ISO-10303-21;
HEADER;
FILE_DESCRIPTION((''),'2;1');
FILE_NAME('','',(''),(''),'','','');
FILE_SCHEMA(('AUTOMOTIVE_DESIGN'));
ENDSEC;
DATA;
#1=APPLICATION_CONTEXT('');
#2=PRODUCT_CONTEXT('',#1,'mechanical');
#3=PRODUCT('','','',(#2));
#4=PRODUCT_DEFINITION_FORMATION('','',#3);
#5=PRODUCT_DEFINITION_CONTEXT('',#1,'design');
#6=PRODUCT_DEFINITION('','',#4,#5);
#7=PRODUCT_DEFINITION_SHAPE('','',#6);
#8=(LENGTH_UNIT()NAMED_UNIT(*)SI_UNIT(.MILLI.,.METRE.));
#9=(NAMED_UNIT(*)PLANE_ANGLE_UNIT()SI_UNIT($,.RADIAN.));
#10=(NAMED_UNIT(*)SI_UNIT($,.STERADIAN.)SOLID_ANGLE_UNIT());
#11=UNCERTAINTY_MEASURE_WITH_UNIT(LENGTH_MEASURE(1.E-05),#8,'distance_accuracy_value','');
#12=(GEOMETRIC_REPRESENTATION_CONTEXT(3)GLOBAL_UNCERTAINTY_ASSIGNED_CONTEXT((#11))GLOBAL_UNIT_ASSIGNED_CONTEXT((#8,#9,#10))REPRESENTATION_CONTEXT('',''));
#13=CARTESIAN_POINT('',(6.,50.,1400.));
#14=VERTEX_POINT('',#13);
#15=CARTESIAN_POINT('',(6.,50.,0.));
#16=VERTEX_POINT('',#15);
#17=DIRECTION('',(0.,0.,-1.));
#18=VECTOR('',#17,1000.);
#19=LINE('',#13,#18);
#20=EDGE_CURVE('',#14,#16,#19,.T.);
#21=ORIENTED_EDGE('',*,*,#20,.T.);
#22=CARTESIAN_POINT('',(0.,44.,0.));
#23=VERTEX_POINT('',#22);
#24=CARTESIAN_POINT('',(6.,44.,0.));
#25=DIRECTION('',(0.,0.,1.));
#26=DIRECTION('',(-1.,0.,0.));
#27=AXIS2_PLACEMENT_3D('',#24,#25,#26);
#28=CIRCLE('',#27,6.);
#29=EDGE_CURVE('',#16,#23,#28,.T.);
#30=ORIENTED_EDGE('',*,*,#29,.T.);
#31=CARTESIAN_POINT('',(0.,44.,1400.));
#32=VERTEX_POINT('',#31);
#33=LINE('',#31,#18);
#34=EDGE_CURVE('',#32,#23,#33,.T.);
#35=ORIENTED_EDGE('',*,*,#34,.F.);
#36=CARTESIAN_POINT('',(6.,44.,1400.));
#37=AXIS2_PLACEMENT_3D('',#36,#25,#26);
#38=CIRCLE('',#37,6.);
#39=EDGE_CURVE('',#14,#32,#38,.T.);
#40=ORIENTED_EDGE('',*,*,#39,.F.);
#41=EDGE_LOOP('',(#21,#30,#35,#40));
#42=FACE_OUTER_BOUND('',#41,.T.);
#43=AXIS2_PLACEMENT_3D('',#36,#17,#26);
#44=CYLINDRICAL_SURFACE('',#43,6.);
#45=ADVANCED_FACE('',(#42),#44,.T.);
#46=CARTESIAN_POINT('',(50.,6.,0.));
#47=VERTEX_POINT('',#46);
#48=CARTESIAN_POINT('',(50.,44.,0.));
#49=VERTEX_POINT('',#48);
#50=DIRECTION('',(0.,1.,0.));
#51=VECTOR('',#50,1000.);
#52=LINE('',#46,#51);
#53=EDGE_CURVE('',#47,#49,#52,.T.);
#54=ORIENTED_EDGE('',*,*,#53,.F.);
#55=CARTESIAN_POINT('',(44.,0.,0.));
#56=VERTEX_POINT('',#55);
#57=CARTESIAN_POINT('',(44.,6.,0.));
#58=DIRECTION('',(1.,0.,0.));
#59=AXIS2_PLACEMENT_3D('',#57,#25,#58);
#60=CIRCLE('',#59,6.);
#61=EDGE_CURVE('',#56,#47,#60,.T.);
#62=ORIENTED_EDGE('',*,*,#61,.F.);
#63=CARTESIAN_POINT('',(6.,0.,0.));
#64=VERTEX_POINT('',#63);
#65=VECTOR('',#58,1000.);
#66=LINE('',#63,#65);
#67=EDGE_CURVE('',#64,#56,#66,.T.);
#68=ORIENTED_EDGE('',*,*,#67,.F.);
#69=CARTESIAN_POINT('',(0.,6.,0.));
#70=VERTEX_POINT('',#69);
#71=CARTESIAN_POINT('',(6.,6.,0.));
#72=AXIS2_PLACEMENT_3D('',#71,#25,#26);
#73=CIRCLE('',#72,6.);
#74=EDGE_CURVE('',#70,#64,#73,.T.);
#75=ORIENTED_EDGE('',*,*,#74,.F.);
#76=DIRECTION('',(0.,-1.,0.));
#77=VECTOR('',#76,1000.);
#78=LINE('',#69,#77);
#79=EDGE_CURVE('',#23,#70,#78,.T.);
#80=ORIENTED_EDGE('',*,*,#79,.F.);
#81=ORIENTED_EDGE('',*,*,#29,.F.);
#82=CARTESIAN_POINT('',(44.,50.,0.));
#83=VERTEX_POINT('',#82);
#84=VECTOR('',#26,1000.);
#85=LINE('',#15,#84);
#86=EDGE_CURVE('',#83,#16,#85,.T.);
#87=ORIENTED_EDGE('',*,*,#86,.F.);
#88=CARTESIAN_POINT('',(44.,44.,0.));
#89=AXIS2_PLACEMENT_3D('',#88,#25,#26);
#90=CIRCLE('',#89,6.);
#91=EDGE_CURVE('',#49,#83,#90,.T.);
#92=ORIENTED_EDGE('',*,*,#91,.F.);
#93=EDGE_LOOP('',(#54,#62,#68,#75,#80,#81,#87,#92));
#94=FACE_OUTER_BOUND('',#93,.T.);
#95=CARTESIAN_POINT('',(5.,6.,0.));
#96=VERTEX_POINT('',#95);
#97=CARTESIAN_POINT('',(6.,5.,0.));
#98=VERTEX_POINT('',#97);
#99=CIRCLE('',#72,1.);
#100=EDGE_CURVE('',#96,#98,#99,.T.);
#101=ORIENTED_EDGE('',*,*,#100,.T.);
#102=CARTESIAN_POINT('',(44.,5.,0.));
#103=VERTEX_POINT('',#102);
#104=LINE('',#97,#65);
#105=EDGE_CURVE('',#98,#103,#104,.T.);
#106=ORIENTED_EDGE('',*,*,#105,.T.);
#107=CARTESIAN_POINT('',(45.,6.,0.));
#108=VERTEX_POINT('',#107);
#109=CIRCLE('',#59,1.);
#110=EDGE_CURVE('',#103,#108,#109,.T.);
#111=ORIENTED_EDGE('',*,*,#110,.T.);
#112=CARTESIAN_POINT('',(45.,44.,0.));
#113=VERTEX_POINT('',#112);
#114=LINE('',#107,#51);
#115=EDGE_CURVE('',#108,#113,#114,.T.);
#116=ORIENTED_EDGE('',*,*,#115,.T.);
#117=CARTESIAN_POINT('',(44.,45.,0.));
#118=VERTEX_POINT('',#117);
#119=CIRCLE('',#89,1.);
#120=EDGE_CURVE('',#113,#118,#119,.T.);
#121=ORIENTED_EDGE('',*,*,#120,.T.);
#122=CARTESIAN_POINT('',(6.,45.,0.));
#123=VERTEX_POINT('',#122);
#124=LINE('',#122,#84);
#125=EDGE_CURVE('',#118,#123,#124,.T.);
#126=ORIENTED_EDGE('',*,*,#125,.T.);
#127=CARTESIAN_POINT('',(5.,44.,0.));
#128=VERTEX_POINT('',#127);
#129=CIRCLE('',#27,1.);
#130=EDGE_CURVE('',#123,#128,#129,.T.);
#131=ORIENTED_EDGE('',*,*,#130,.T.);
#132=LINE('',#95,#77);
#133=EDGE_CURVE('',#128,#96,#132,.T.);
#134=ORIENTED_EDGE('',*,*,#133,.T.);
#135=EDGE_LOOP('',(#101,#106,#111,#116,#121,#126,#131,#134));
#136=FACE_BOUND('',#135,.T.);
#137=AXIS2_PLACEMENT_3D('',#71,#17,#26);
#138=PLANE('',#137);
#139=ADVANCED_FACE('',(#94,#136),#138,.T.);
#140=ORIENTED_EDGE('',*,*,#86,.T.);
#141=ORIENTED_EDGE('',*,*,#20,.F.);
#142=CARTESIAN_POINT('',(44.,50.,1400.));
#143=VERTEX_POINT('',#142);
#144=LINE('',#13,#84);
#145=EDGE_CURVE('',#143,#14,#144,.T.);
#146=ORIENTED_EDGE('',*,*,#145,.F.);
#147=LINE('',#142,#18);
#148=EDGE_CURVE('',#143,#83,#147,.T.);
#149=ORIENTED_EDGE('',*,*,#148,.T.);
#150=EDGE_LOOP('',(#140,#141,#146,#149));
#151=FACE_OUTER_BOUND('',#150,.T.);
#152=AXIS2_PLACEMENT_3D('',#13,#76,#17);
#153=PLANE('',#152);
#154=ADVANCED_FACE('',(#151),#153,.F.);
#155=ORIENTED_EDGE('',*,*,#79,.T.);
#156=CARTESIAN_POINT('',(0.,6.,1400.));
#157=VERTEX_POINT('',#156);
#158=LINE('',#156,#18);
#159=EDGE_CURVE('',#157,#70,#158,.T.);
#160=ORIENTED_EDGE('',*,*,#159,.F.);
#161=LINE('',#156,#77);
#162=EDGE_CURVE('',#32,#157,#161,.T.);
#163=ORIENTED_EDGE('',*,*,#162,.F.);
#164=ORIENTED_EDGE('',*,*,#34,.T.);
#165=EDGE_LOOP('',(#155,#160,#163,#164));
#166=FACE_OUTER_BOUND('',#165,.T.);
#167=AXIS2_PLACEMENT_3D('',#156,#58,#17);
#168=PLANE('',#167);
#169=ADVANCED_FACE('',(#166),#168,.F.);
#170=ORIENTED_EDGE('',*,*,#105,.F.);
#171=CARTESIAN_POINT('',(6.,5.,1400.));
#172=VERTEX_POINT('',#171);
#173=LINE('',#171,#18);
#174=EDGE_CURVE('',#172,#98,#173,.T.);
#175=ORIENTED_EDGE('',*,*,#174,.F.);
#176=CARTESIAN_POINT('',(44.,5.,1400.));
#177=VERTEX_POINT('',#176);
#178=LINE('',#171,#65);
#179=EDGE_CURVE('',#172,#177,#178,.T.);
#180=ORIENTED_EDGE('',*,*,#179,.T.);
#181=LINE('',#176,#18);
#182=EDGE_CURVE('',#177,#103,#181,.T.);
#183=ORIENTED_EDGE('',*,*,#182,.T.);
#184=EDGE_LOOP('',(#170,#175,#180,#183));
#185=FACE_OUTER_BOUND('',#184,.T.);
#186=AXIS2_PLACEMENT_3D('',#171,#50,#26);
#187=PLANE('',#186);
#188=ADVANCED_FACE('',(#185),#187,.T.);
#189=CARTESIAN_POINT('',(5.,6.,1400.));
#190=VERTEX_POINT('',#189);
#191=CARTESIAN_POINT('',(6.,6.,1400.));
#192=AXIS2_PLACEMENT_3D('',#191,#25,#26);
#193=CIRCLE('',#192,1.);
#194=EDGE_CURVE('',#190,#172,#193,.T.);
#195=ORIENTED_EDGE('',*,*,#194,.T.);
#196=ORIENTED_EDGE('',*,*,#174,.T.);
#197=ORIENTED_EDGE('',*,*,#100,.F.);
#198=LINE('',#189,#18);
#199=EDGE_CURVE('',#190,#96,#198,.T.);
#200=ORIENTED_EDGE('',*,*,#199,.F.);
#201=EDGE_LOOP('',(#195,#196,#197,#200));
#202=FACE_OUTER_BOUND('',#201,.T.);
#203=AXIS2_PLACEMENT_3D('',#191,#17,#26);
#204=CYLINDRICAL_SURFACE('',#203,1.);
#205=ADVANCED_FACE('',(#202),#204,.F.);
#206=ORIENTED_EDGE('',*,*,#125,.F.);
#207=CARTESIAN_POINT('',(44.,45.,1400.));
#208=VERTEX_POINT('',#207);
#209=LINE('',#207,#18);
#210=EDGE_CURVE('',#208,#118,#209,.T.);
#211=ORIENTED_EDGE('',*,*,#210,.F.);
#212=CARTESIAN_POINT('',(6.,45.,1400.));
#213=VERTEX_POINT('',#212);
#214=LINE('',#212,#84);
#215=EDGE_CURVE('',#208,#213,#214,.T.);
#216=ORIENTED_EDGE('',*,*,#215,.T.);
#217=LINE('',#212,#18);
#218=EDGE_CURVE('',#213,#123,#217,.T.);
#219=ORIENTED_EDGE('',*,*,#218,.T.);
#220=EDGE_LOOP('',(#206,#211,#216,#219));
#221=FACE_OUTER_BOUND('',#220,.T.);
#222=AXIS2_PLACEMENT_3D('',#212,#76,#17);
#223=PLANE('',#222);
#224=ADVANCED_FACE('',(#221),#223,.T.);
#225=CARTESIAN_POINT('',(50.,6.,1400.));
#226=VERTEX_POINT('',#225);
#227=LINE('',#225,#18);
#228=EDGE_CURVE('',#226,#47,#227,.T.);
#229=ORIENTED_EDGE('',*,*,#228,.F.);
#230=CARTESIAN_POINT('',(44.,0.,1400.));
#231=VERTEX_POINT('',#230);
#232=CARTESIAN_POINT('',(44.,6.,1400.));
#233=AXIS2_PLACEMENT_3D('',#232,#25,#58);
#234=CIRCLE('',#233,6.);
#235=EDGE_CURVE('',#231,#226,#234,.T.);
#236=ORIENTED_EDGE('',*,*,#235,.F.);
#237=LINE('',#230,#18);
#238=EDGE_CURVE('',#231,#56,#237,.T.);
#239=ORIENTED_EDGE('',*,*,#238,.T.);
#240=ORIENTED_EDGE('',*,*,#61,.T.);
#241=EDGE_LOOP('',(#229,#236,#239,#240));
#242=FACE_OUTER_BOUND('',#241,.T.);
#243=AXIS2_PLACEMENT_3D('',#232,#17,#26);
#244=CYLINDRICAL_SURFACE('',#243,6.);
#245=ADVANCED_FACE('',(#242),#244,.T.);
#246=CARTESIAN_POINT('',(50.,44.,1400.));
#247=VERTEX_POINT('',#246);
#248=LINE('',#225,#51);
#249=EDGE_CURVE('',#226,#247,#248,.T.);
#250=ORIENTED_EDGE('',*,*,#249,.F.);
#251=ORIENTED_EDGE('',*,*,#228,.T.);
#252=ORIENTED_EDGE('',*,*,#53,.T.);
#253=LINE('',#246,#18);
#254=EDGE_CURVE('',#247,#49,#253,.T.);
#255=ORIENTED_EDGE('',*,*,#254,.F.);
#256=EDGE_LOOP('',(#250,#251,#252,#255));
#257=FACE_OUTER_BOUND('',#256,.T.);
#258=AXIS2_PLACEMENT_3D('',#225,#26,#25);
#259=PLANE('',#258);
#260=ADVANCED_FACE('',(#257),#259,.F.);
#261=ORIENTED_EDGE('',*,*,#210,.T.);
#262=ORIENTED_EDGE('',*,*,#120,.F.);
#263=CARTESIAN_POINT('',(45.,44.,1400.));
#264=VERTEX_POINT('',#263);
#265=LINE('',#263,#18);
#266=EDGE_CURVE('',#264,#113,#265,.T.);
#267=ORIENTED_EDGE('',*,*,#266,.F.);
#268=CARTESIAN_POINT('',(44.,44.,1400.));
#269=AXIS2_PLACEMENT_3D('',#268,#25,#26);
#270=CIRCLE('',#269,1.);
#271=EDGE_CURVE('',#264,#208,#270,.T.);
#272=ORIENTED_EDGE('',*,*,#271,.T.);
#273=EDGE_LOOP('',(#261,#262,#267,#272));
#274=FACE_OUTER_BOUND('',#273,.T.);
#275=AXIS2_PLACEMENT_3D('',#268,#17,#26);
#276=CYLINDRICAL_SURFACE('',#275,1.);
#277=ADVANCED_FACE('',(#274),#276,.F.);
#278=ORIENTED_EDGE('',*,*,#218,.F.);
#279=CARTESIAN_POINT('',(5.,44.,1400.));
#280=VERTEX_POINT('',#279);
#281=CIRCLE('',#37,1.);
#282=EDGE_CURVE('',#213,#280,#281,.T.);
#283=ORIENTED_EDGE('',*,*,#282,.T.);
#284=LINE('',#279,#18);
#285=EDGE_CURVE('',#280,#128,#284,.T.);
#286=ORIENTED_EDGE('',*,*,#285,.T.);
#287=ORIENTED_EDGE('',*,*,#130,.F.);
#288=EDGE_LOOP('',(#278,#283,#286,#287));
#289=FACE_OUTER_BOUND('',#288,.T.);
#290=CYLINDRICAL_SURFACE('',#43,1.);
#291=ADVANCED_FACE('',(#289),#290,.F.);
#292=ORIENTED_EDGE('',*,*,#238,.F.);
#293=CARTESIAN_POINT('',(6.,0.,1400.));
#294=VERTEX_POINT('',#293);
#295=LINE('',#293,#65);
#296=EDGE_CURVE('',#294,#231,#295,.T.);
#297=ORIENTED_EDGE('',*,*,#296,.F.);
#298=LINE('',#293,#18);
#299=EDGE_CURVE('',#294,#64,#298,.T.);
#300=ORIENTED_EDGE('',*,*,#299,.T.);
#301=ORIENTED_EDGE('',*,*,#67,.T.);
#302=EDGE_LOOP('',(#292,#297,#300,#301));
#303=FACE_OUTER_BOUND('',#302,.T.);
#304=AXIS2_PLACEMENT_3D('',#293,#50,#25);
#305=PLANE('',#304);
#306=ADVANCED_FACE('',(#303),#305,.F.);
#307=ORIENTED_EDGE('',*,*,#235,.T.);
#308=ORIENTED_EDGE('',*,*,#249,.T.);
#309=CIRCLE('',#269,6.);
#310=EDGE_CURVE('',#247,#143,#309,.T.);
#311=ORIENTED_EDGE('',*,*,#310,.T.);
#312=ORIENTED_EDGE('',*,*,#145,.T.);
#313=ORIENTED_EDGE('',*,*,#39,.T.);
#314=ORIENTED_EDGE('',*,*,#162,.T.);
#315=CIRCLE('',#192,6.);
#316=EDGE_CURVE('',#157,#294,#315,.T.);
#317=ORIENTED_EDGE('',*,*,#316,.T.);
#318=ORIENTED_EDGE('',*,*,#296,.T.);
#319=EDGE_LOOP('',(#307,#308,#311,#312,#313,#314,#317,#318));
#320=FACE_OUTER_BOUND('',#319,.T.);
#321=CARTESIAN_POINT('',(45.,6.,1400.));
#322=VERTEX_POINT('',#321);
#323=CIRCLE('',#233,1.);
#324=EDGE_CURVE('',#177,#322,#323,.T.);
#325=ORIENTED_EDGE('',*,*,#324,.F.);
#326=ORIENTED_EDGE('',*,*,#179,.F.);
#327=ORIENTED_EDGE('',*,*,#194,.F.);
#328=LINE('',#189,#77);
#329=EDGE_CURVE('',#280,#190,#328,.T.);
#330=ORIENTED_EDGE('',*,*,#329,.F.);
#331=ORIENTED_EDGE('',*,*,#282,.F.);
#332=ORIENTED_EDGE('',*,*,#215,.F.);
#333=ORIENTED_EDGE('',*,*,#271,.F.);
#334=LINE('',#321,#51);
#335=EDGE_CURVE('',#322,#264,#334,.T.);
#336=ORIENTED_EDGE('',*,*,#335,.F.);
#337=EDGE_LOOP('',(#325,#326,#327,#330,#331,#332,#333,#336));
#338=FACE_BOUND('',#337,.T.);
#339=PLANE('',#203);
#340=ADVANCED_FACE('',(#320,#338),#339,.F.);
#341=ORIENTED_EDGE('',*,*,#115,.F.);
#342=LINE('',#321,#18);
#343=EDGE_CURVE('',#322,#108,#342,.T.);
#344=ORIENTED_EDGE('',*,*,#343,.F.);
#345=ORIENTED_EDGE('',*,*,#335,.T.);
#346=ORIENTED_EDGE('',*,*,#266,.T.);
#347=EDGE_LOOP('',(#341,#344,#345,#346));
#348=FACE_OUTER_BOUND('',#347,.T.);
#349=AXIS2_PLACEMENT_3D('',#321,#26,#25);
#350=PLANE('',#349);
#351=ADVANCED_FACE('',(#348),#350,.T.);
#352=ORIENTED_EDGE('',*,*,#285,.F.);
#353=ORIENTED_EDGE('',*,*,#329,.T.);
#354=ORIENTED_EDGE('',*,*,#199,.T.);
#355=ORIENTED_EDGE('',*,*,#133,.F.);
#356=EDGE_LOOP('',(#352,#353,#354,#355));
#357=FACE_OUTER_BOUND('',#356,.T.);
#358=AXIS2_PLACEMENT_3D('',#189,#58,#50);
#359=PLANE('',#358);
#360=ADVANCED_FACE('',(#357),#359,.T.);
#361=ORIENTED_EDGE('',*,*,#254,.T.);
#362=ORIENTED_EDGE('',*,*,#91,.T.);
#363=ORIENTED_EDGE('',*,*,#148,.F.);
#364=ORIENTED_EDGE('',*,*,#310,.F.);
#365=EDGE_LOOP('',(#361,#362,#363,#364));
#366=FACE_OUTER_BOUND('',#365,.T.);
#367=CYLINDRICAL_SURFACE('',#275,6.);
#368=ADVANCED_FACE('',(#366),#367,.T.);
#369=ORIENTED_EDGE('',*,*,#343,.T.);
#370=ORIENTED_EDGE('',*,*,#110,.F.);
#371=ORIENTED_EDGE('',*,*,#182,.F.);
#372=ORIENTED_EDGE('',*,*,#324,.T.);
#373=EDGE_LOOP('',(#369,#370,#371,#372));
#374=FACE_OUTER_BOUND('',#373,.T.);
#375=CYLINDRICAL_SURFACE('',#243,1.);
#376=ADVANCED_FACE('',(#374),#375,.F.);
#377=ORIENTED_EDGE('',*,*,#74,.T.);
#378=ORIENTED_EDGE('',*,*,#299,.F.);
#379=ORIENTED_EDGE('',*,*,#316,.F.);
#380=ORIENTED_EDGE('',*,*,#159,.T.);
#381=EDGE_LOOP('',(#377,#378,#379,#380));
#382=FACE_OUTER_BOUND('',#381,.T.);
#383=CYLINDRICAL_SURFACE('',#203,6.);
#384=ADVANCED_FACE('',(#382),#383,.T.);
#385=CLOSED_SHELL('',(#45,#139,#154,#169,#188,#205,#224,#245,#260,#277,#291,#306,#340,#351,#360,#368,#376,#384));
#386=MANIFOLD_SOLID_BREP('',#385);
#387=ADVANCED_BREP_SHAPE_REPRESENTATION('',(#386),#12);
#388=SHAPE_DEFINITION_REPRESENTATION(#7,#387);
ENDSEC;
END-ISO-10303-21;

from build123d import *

# Parameters (mm, degrees)
BOSS_EXTRUDE1_DEPTH = 1400


with BuildPart() as part:
    # Sketch1 → Boss-Extrude1 (new body)
    with BuildSketch(Plane.XY):
        with BuildLine():
            Line((6, 0), (44, 0))
            ThreePointArc((44, 0), (48.242640687, 1.757359313), (50, 6))
            Line((50, 6), (50, 44))
            ThreePointArc((50, 44), (48.242640687, 48.242640687), (44, 50))
            Line((44, 50), (6, 50))
            ThreePointArc((6, 50), (1.757359313, 48.242640687), (0, 44))
            Line((0, 44), (0, 6))
            ThreePointArc((0, 6), (1.757359313, 1.757359313), (6, 0))
        make_face()
        with BuildLine():
            Line((6, 45), (44, 45))
            ThreePointArc((44, 45), (44.707106781, 44.707106781), (45, 44))
            Line((45, 44), (45, 6))
            ThreePointArc((45, 6), (44.707106781, 5.292893219), (44, 5))
            Line((44, 5), (6, 5))
            ThreePointArc((6, 5), (5.292893219, 5.292893219), (5, 6))
            Line((5, 6), (5, 44))
            ThreePointArc((5, 44), (5.292893219, 44.707106781), (6, 45))
        make_face(mode=Mode.SUBTRACT)
    extrude(amount=BOSS_EXTRUDE1_DEPTH)


solid = part.part
